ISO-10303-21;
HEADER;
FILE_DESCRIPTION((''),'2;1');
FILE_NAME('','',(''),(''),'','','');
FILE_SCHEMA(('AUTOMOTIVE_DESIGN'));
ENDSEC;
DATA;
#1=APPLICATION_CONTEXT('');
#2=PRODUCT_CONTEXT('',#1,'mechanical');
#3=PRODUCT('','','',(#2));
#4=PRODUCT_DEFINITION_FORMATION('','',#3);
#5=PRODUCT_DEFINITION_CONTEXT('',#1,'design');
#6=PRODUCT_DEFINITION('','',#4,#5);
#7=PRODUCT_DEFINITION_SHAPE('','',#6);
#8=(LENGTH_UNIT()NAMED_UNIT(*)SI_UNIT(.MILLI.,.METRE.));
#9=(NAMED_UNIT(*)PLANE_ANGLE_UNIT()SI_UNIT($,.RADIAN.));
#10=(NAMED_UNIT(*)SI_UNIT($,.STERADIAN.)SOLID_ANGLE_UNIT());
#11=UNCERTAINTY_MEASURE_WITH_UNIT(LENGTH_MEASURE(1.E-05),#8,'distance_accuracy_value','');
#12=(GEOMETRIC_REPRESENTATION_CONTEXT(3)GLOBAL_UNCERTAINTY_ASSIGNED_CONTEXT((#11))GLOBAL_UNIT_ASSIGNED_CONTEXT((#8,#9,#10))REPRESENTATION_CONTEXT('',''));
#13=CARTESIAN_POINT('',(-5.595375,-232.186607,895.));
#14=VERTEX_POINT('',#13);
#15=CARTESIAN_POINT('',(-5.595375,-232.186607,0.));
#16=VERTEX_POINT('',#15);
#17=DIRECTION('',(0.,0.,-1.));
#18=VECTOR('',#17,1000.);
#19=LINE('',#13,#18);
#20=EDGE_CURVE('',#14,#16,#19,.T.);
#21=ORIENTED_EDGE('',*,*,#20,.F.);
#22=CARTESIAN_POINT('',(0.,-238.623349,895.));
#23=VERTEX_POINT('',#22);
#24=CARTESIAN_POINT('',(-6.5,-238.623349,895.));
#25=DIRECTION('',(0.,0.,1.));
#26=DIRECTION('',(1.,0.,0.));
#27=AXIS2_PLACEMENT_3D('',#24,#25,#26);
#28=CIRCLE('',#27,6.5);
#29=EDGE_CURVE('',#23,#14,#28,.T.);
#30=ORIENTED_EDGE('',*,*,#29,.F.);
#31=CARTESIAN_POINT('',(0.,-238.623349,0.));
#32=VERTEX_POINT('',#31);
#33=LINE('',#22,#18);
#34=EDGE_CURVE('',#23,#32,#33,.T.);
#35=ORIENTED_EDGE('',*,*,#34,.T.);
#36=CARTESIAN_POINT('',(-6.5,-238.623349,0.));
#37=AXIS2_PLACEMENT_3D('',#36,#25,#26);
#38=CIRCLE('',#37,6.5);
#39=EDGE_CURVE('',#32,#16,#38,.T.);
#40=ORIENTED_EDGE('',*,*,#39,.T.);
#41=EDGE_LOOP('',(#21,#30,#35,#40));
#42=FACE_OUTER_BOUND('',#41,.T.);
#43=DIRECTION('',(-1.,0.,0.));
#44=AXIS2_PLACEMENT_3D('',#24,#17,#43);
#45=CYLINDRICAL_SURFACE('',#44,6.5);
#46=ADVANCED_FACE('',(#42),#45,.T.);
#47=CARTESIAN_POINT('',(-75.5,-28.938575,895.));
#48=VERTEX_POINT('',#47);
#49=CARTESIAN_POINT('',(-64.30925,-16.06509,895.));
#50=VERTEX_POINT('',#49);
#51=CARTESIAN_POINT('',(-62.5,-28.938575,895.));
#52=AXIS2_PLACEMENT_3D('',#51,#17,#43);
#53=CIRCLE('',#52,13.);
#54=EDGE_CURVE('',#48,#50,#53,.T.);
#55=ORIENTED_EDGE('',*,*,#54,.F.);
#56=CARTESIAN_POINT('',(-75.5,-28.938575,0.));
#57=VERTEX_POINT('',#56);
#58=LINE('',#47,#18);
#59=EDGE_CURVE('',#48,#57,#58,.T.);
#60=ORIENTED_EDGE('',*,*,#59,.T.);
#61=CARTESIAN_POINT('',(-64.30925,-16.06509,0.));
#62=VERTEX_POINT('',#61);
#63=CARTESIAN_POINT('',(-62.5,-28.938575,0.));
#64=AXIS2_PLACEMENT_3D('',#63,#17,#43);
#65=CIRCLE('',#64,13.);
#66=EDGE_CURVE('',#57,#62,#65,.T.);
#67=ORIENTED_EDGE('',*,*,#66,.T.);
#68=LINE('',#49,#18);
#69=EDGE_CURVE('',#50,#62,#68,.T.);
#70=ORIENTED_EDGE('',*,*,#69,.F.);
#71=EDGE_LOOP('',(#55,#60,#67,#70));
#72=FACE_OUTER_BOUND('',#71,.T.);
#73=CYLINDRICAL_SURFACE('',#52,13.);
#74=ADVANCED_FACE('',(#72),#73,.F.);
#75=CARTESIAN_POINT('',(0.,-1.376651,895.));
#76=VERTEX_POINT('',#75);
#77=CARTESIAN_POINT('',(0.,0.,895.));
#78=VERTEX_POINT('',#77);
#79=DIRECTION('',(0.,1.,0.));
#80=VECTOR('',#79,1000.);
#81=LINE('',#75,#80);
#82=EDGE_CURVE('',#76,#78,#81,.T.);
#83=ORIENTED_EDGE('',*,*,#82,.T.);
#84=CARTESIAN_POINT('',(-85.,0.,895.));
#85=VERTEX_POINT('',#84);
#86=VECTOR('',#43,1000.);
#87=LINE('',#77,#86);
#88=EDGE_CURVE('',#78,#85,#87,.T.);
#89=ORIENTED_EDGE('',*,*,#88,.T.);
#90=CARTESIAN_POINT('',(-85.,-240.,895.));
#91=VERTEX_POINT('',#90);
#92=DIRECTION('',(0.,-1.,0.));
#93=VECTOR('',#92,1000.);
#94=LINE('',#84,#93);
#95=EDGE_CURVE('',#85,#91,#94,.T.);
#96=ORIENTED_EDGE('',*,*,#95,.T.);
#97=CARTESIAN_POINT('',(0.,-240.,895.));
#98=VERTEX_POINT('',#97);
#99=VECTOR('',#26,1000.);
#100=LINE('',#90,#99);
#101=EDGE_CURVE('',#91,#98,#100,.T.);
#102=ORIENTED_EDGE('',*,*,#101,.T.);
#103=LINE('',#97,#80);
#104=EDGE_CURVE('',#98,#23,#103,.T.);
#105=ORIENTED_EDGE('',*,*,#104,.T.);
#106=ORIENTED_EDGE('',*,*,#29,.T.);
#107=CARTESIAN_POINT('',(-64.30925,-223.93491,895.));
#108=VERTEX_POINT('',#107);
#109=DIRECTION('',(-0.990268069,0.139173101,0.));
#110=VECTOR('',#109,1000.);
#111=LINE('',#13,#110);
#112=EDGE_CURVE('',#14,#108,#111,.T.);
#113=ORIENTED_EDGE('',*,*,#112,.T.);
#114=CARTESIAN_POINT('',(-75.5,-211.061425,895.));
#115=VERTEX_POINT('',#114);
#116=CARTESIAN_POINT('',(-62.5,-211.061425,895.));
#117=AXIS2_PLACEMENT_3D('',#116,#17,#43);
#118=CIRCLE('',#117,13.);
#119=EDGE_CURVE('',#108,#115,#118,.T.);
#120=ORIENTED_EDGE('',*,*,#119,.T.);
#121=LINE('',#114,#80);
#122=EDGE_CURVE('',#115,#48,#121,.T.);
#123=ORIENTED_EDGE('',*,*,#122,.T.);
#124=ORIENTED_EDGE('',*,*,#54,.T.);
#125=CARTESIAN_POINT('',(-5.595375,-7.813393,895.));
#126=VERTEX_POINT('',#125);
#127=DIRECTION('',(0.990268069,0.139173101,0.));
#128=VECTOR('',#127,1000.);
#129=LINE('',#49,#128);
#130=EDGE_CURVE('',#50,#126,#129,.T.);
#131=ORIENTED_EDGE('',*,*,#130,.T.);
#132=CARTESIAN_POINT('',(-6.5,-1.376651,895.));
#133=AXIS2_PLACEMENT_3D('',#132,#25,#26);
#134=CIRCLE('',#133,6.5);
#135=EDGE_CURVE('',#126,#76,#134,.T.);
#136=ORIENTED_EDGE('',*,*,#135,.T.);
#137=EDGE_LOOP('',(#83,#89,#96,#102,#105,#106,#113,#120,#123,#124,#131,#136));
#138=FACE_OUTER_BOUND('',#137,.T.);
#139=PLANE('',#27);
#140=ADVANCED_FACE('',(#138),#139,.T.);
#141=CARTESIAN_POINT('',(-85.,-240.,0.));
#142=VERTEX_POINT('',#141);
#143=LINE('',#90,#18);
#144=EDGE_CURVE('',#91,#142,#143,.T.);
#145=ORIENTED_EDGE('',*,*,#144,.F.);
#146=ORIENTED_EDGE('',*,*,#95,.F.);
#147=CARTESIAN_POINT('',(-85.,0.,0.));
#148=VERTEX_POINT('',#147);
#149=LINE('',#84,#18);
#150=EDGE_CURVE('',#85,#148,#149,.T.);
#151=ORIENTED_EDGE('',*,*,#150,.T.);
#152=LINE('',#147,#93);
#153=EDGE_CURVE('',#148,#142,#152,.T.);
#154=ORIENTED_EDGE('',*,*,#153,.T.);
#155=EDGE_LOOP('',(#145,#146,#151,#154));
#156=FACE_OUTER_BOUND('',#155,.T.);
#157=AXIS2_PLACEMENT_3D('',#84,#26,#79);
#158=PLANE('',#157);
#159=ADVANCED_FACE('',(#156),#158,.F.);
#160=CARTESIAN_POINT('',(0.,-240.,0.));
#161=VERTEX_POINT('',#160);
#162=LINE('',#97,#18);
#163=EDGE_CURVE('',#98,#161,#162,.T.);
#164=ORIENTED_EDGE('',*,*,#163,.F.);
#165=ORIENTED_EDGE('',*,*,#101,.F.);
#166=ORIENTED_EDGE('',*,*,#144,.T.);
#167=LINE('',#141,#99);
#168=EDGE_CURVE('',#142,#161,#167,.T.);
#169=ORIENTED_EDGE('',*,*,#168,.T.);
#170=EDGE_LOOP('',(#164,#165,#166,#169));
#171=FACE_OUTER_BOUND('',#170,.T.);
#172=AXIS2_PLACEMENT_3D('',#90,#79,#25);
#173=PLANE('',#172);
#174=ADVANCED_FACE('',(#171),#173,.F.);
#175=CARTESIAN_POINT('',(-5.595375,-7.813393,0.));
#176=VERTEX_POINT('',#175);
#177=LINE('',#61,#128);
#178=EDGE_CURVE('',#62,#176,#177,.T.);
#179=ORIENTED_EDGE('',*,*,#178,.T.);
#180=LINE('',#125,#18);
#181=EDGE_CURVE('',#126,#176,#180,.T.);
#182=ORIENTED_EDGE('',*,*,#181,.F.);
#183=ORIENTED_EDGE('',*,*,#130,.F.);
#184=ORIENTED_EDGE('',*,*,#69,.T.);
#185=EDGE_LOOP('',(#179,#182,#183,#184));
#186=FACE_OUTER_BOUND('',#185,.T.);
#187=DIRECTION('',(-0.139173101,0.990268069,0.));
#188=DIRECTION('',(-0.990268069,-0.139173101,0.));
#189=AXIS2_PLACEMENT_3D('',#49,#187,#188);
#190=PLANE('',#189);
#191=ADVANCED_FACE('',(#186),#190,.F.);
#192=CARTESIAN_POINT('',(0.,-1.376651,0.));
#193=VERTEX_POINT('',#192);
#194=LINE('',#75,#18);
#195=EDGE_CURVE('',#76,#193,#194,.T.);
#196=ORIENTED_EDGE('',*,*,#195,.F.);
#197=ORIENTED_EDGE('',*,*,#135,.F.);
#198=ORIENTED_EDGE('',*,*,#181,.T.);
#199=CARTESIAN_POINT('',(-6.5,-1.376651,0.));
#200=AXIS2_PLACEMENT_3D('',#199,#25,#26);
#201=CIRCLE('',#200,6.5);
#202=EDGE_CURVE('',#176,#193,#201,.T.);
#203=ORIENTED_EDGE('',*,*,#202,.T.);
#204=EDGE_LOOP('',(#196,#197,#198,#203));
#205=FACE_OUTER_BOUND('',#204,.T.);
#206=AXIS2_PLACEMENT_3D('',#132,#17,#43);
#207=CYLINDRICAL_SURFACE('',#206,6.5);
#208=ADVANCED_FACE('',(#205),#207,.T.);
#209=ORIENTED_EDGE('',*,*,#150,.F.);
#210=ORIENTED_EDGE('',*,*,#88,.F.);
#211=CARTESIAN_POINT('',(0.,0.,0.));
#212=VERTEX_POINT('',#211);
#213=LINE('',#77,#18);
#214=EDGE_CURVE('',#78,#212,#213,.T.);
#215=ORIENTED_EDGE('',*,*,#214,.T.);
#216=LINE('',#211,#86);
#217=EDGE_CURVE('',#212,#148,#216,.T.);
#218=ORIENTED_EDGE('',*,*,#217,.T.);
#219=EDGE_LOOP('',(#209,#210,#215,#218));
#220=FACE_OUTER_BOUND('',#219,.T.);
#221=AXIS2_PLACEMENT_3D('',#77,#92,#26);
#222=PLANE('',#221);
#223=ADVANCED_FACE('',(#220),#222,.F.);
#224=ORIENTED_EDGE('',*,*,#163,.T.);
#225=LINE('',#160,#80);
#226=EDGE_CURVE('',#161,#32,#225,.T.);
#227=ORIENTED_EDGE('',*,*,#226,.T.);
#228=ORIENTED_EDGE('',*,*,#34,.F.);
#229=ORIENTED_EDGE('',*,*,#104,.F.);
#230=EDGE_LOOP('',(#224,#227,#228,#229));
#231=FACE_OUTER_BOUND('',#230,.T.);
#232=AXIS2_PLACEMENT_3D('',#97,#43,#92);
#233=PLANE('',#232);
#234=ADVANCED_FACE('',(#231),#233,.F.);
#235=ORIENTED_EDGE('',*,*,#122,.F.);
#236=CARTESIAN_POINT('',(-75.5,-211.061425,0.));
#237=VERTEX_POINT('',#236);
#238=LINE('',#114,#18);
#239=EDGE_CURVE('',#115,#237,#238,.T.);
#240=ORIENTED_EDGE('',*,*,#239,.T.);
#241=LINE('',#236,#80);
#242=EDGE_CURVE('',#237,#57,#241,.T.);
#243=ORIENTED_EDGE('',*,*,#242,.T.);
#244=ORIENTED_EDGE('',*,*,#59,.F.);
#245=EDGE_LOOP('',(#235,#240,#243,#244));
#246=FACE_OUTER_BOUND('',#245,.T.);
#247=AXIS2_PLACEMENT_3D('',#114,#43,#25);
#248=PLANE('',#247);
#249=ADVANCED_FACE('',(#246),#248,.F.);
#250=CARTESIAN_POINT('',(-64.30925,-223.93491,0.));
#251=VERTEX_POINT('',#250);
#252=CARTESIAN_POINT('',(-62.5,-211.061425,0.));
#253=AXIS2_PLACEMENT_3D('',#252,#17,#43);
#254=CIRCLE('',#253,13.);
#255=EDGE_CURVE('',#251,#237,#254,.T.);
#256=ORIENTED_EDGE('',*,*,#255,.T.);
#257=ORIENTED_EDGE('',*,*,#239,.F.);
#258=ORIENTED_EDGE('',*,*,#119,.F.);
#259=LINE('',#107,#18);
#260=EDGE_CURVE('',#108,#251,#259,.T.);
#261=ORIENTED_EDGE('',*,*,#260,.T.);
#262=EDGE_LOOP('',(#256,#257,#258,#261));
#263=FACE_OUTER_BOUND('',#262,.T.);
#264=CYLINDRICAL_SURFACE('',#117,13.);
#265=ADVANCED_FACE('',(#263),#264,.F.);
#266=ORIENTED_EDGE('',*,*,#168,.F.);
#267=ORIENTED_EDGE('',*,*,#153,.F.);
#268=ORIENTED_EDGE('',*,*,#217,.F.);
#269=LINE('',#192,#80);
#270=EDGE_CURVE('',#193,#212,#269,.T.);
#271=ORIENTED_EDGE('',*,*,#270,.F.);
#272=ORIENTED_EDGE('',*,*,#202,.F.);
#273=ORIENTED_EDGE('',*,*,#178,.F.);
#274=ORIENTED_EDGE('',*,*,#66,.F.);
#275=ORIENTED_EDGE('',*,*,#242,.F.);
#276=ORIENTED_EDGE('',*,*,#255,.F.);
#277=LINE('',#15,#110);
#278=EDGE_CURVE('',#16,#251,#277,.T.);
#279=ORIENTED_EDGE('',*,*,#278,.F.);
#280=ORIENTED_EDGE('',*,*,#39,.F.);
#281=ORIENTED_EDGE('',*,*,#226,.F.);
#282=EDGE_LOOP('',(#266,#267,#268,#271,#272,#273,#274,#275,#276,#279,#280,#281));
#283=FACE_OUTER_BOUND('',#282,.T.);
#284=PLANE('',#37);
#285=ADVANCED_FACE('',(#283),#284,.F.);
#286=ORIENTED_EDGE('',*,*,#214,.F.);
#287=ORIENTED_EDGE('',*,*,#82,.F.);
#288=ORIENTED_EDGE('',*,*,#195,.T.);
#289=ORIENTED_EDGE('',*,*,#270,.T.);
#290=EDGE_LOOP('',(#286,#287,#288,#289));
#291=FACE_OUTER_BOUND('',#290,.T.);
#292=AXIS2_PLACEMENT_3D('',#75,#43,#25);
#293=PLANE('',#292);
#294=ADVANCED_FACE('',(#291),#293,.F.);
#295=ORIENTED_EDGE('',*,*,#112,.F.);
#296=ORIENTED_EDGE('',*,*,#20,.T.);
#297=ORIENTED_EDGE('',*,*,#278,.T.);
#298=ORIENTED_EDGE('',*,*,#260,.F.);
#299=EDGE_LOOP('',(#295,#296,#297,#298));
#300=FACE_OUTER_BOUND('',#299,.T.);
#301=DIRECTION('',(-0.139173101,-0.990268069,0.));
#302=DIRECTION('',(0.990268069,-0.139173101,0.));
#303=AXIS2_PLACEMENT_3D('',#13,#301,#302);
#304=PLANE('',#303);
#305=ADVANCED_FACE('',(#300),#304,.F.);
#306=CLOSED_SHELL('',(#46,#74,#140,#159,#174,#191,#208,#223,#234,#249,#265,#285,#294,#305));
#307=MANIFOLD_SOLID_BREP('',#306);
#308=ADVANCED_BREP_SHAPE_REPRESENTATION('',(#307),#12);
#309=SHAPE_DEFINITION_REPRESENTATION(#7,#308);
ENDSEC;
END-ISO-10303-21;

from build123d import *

# Parameters (mm, degrees)
EXTRUDE_1_DEPTH = 895


with BuildPart() as part:
    # 草图1 → 凸台-拉伸1 (new body)
    with BuildSketch(Plane.XY):
        with BuildLine():
            Line((0, 0), (-85, 0))
            Line((-85, 0), (-85, -240))
            Line((-85, -240), (0, -240))
            Line((0, -240), (0, -238.623349271))
            ThreePointArc((0, -238.623349271), (-1.594387729, -234.358965582), (-5.595374844, -232.186606824))
            Line((-5.595374844, -232.186606824), (-64.309250312, -223.934909757))
            ThreePointArc((-64.309250312, -223.934909757), (-72.311224543, -219.59019224), (-75.5, -211.061424863))
            Line((-75.5, -211.061424863), (-75.5, -28.938575137))
            ThreePointArc((-75.5, -28.938575137), (-72.311224543, -20.40980776), (-64.309250312, -16.065090243))
            Line((-64.309250312, -16.065090243), (-5.595374844, -7.813393176))
            ThreePointArc((-5.595374844, -7.813393176), (-1.594387729, -5.641034418), (0, -1.376650729))
            Line((0, -1.376650729), (0, 0))
        make_face()
    extrude(amount=EXTRUDE_1_DEPTH)


solid = part.part
